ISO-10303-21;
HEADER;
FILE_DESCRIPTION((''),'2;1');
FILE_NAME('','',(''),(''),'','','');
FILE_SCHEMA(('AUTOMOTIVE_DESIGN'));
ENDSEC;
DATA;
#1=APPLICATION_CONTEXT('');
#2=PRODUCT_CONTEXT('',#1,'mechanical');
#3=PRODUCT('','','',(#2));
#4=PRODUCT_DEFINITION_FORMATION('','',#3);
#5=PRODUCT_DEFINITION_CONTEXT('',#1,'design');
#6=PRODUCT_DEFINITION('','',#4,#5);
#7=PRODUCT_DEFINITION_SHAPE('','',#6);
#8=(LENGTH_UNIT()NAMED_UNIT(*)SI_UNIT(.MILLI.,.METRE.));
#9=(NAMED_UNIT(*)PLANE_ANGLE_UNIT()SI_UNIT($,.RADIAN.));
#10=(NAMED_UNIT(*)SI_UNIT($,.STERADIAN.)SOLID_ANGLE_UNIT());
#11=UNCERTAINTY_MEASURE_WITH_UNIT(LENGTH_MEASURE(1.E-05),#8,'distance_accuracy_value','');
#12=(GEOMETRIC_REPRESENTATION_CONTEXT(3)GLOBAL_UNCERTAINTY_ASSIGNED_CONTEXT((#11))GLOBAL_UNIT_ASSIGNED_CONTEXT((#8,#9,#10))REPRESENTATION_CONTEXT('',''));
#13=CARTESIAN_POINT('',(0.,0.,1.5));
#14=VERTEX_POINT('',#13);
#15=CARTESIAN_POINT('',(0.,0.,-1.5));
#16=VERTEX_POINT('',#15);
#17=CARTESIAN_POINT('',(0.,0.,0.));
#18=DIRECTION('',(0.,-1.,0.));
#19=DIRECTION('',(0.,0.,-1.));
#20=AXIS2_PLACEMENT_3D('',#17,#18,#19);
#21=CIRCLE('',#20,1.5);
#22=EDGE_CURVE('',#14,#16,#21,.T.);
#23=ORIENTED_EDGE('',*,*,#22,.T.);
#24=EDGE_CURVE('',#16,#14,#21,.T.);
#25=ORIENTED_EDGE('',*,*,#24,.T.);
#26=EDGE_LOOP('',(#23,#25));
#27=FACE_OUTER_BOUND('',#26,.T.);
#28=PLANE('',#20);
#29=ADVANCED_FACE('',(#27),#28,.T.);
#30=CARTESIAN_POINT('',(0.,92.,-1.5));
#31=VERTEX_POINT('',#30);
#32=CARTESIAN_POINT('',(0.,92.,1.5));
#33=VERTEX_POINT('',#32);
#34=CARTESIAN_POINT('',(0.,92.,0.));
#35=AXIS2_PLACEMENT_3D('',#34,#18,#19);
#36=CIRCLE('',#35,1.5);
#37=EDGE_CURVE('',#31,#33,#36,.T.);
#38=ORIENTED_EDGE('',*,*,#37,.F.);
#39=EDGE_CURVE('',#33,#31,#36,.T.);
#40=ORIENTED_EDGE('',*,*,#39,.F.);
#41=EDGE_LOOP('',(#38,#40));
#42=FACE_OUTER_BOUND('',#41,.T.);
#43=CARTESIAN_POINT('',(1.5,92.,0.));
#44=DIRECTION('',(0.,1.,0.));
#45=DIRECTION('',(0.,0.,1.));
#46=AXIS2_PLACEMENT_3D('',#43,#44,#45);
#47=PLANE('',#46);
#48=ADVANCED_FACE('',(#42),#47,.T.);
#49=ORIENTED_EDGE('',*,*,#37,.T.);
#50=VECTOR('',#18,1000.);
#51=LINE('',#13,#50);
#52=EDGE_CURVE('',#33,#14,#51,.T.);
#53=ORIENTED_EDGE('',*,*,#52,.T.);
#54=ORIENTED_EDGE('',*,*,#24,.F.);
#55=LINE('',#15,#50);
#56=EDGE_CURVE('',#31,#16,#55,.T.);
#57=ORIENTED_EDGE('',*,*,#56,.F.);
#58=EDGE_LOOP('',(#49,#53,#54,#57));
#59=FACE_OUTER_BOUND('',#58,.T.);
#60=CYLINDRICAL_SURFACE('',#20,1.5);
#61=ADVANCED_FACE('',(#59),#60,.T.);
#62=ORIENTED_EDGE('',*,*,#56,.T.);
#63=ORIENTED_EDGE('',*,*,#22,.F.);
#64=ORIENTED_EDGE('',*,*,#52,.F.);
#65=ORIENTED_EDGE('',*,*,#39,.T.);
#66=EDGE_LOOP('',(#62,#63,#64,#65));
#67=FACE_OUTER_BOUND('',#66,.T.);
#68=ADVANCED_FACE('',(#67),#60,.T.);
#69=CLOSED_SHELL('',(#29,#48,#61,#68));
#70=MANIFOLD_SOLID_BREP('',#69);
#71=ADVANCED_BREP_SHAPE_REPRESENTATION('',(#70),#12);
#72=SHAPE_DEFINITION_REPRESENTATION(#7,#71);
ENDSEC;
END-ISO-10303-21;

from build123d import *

# Parameters (mm, degrees)
SKETCH1_W = 1.5
SKETCH1_H = 92


with BuildPart() as part:
    # Sketch1 → Revolve1 (revolve)
    with BuildSketch(Plane.XY, mode=Mode.PRIVATE) as revolve1_sk:
        with Locations((0.75, 46)):
            Rectangle(SKETCH1_W, SKETCH1_H)
    revolve(revolve1_sk.sketch.rotate(Axis((0, 0, 0), (0, 1, 0)), 90), axis=Axis((0, 0, 0), (0, 1, 0)))


solid = part.part
